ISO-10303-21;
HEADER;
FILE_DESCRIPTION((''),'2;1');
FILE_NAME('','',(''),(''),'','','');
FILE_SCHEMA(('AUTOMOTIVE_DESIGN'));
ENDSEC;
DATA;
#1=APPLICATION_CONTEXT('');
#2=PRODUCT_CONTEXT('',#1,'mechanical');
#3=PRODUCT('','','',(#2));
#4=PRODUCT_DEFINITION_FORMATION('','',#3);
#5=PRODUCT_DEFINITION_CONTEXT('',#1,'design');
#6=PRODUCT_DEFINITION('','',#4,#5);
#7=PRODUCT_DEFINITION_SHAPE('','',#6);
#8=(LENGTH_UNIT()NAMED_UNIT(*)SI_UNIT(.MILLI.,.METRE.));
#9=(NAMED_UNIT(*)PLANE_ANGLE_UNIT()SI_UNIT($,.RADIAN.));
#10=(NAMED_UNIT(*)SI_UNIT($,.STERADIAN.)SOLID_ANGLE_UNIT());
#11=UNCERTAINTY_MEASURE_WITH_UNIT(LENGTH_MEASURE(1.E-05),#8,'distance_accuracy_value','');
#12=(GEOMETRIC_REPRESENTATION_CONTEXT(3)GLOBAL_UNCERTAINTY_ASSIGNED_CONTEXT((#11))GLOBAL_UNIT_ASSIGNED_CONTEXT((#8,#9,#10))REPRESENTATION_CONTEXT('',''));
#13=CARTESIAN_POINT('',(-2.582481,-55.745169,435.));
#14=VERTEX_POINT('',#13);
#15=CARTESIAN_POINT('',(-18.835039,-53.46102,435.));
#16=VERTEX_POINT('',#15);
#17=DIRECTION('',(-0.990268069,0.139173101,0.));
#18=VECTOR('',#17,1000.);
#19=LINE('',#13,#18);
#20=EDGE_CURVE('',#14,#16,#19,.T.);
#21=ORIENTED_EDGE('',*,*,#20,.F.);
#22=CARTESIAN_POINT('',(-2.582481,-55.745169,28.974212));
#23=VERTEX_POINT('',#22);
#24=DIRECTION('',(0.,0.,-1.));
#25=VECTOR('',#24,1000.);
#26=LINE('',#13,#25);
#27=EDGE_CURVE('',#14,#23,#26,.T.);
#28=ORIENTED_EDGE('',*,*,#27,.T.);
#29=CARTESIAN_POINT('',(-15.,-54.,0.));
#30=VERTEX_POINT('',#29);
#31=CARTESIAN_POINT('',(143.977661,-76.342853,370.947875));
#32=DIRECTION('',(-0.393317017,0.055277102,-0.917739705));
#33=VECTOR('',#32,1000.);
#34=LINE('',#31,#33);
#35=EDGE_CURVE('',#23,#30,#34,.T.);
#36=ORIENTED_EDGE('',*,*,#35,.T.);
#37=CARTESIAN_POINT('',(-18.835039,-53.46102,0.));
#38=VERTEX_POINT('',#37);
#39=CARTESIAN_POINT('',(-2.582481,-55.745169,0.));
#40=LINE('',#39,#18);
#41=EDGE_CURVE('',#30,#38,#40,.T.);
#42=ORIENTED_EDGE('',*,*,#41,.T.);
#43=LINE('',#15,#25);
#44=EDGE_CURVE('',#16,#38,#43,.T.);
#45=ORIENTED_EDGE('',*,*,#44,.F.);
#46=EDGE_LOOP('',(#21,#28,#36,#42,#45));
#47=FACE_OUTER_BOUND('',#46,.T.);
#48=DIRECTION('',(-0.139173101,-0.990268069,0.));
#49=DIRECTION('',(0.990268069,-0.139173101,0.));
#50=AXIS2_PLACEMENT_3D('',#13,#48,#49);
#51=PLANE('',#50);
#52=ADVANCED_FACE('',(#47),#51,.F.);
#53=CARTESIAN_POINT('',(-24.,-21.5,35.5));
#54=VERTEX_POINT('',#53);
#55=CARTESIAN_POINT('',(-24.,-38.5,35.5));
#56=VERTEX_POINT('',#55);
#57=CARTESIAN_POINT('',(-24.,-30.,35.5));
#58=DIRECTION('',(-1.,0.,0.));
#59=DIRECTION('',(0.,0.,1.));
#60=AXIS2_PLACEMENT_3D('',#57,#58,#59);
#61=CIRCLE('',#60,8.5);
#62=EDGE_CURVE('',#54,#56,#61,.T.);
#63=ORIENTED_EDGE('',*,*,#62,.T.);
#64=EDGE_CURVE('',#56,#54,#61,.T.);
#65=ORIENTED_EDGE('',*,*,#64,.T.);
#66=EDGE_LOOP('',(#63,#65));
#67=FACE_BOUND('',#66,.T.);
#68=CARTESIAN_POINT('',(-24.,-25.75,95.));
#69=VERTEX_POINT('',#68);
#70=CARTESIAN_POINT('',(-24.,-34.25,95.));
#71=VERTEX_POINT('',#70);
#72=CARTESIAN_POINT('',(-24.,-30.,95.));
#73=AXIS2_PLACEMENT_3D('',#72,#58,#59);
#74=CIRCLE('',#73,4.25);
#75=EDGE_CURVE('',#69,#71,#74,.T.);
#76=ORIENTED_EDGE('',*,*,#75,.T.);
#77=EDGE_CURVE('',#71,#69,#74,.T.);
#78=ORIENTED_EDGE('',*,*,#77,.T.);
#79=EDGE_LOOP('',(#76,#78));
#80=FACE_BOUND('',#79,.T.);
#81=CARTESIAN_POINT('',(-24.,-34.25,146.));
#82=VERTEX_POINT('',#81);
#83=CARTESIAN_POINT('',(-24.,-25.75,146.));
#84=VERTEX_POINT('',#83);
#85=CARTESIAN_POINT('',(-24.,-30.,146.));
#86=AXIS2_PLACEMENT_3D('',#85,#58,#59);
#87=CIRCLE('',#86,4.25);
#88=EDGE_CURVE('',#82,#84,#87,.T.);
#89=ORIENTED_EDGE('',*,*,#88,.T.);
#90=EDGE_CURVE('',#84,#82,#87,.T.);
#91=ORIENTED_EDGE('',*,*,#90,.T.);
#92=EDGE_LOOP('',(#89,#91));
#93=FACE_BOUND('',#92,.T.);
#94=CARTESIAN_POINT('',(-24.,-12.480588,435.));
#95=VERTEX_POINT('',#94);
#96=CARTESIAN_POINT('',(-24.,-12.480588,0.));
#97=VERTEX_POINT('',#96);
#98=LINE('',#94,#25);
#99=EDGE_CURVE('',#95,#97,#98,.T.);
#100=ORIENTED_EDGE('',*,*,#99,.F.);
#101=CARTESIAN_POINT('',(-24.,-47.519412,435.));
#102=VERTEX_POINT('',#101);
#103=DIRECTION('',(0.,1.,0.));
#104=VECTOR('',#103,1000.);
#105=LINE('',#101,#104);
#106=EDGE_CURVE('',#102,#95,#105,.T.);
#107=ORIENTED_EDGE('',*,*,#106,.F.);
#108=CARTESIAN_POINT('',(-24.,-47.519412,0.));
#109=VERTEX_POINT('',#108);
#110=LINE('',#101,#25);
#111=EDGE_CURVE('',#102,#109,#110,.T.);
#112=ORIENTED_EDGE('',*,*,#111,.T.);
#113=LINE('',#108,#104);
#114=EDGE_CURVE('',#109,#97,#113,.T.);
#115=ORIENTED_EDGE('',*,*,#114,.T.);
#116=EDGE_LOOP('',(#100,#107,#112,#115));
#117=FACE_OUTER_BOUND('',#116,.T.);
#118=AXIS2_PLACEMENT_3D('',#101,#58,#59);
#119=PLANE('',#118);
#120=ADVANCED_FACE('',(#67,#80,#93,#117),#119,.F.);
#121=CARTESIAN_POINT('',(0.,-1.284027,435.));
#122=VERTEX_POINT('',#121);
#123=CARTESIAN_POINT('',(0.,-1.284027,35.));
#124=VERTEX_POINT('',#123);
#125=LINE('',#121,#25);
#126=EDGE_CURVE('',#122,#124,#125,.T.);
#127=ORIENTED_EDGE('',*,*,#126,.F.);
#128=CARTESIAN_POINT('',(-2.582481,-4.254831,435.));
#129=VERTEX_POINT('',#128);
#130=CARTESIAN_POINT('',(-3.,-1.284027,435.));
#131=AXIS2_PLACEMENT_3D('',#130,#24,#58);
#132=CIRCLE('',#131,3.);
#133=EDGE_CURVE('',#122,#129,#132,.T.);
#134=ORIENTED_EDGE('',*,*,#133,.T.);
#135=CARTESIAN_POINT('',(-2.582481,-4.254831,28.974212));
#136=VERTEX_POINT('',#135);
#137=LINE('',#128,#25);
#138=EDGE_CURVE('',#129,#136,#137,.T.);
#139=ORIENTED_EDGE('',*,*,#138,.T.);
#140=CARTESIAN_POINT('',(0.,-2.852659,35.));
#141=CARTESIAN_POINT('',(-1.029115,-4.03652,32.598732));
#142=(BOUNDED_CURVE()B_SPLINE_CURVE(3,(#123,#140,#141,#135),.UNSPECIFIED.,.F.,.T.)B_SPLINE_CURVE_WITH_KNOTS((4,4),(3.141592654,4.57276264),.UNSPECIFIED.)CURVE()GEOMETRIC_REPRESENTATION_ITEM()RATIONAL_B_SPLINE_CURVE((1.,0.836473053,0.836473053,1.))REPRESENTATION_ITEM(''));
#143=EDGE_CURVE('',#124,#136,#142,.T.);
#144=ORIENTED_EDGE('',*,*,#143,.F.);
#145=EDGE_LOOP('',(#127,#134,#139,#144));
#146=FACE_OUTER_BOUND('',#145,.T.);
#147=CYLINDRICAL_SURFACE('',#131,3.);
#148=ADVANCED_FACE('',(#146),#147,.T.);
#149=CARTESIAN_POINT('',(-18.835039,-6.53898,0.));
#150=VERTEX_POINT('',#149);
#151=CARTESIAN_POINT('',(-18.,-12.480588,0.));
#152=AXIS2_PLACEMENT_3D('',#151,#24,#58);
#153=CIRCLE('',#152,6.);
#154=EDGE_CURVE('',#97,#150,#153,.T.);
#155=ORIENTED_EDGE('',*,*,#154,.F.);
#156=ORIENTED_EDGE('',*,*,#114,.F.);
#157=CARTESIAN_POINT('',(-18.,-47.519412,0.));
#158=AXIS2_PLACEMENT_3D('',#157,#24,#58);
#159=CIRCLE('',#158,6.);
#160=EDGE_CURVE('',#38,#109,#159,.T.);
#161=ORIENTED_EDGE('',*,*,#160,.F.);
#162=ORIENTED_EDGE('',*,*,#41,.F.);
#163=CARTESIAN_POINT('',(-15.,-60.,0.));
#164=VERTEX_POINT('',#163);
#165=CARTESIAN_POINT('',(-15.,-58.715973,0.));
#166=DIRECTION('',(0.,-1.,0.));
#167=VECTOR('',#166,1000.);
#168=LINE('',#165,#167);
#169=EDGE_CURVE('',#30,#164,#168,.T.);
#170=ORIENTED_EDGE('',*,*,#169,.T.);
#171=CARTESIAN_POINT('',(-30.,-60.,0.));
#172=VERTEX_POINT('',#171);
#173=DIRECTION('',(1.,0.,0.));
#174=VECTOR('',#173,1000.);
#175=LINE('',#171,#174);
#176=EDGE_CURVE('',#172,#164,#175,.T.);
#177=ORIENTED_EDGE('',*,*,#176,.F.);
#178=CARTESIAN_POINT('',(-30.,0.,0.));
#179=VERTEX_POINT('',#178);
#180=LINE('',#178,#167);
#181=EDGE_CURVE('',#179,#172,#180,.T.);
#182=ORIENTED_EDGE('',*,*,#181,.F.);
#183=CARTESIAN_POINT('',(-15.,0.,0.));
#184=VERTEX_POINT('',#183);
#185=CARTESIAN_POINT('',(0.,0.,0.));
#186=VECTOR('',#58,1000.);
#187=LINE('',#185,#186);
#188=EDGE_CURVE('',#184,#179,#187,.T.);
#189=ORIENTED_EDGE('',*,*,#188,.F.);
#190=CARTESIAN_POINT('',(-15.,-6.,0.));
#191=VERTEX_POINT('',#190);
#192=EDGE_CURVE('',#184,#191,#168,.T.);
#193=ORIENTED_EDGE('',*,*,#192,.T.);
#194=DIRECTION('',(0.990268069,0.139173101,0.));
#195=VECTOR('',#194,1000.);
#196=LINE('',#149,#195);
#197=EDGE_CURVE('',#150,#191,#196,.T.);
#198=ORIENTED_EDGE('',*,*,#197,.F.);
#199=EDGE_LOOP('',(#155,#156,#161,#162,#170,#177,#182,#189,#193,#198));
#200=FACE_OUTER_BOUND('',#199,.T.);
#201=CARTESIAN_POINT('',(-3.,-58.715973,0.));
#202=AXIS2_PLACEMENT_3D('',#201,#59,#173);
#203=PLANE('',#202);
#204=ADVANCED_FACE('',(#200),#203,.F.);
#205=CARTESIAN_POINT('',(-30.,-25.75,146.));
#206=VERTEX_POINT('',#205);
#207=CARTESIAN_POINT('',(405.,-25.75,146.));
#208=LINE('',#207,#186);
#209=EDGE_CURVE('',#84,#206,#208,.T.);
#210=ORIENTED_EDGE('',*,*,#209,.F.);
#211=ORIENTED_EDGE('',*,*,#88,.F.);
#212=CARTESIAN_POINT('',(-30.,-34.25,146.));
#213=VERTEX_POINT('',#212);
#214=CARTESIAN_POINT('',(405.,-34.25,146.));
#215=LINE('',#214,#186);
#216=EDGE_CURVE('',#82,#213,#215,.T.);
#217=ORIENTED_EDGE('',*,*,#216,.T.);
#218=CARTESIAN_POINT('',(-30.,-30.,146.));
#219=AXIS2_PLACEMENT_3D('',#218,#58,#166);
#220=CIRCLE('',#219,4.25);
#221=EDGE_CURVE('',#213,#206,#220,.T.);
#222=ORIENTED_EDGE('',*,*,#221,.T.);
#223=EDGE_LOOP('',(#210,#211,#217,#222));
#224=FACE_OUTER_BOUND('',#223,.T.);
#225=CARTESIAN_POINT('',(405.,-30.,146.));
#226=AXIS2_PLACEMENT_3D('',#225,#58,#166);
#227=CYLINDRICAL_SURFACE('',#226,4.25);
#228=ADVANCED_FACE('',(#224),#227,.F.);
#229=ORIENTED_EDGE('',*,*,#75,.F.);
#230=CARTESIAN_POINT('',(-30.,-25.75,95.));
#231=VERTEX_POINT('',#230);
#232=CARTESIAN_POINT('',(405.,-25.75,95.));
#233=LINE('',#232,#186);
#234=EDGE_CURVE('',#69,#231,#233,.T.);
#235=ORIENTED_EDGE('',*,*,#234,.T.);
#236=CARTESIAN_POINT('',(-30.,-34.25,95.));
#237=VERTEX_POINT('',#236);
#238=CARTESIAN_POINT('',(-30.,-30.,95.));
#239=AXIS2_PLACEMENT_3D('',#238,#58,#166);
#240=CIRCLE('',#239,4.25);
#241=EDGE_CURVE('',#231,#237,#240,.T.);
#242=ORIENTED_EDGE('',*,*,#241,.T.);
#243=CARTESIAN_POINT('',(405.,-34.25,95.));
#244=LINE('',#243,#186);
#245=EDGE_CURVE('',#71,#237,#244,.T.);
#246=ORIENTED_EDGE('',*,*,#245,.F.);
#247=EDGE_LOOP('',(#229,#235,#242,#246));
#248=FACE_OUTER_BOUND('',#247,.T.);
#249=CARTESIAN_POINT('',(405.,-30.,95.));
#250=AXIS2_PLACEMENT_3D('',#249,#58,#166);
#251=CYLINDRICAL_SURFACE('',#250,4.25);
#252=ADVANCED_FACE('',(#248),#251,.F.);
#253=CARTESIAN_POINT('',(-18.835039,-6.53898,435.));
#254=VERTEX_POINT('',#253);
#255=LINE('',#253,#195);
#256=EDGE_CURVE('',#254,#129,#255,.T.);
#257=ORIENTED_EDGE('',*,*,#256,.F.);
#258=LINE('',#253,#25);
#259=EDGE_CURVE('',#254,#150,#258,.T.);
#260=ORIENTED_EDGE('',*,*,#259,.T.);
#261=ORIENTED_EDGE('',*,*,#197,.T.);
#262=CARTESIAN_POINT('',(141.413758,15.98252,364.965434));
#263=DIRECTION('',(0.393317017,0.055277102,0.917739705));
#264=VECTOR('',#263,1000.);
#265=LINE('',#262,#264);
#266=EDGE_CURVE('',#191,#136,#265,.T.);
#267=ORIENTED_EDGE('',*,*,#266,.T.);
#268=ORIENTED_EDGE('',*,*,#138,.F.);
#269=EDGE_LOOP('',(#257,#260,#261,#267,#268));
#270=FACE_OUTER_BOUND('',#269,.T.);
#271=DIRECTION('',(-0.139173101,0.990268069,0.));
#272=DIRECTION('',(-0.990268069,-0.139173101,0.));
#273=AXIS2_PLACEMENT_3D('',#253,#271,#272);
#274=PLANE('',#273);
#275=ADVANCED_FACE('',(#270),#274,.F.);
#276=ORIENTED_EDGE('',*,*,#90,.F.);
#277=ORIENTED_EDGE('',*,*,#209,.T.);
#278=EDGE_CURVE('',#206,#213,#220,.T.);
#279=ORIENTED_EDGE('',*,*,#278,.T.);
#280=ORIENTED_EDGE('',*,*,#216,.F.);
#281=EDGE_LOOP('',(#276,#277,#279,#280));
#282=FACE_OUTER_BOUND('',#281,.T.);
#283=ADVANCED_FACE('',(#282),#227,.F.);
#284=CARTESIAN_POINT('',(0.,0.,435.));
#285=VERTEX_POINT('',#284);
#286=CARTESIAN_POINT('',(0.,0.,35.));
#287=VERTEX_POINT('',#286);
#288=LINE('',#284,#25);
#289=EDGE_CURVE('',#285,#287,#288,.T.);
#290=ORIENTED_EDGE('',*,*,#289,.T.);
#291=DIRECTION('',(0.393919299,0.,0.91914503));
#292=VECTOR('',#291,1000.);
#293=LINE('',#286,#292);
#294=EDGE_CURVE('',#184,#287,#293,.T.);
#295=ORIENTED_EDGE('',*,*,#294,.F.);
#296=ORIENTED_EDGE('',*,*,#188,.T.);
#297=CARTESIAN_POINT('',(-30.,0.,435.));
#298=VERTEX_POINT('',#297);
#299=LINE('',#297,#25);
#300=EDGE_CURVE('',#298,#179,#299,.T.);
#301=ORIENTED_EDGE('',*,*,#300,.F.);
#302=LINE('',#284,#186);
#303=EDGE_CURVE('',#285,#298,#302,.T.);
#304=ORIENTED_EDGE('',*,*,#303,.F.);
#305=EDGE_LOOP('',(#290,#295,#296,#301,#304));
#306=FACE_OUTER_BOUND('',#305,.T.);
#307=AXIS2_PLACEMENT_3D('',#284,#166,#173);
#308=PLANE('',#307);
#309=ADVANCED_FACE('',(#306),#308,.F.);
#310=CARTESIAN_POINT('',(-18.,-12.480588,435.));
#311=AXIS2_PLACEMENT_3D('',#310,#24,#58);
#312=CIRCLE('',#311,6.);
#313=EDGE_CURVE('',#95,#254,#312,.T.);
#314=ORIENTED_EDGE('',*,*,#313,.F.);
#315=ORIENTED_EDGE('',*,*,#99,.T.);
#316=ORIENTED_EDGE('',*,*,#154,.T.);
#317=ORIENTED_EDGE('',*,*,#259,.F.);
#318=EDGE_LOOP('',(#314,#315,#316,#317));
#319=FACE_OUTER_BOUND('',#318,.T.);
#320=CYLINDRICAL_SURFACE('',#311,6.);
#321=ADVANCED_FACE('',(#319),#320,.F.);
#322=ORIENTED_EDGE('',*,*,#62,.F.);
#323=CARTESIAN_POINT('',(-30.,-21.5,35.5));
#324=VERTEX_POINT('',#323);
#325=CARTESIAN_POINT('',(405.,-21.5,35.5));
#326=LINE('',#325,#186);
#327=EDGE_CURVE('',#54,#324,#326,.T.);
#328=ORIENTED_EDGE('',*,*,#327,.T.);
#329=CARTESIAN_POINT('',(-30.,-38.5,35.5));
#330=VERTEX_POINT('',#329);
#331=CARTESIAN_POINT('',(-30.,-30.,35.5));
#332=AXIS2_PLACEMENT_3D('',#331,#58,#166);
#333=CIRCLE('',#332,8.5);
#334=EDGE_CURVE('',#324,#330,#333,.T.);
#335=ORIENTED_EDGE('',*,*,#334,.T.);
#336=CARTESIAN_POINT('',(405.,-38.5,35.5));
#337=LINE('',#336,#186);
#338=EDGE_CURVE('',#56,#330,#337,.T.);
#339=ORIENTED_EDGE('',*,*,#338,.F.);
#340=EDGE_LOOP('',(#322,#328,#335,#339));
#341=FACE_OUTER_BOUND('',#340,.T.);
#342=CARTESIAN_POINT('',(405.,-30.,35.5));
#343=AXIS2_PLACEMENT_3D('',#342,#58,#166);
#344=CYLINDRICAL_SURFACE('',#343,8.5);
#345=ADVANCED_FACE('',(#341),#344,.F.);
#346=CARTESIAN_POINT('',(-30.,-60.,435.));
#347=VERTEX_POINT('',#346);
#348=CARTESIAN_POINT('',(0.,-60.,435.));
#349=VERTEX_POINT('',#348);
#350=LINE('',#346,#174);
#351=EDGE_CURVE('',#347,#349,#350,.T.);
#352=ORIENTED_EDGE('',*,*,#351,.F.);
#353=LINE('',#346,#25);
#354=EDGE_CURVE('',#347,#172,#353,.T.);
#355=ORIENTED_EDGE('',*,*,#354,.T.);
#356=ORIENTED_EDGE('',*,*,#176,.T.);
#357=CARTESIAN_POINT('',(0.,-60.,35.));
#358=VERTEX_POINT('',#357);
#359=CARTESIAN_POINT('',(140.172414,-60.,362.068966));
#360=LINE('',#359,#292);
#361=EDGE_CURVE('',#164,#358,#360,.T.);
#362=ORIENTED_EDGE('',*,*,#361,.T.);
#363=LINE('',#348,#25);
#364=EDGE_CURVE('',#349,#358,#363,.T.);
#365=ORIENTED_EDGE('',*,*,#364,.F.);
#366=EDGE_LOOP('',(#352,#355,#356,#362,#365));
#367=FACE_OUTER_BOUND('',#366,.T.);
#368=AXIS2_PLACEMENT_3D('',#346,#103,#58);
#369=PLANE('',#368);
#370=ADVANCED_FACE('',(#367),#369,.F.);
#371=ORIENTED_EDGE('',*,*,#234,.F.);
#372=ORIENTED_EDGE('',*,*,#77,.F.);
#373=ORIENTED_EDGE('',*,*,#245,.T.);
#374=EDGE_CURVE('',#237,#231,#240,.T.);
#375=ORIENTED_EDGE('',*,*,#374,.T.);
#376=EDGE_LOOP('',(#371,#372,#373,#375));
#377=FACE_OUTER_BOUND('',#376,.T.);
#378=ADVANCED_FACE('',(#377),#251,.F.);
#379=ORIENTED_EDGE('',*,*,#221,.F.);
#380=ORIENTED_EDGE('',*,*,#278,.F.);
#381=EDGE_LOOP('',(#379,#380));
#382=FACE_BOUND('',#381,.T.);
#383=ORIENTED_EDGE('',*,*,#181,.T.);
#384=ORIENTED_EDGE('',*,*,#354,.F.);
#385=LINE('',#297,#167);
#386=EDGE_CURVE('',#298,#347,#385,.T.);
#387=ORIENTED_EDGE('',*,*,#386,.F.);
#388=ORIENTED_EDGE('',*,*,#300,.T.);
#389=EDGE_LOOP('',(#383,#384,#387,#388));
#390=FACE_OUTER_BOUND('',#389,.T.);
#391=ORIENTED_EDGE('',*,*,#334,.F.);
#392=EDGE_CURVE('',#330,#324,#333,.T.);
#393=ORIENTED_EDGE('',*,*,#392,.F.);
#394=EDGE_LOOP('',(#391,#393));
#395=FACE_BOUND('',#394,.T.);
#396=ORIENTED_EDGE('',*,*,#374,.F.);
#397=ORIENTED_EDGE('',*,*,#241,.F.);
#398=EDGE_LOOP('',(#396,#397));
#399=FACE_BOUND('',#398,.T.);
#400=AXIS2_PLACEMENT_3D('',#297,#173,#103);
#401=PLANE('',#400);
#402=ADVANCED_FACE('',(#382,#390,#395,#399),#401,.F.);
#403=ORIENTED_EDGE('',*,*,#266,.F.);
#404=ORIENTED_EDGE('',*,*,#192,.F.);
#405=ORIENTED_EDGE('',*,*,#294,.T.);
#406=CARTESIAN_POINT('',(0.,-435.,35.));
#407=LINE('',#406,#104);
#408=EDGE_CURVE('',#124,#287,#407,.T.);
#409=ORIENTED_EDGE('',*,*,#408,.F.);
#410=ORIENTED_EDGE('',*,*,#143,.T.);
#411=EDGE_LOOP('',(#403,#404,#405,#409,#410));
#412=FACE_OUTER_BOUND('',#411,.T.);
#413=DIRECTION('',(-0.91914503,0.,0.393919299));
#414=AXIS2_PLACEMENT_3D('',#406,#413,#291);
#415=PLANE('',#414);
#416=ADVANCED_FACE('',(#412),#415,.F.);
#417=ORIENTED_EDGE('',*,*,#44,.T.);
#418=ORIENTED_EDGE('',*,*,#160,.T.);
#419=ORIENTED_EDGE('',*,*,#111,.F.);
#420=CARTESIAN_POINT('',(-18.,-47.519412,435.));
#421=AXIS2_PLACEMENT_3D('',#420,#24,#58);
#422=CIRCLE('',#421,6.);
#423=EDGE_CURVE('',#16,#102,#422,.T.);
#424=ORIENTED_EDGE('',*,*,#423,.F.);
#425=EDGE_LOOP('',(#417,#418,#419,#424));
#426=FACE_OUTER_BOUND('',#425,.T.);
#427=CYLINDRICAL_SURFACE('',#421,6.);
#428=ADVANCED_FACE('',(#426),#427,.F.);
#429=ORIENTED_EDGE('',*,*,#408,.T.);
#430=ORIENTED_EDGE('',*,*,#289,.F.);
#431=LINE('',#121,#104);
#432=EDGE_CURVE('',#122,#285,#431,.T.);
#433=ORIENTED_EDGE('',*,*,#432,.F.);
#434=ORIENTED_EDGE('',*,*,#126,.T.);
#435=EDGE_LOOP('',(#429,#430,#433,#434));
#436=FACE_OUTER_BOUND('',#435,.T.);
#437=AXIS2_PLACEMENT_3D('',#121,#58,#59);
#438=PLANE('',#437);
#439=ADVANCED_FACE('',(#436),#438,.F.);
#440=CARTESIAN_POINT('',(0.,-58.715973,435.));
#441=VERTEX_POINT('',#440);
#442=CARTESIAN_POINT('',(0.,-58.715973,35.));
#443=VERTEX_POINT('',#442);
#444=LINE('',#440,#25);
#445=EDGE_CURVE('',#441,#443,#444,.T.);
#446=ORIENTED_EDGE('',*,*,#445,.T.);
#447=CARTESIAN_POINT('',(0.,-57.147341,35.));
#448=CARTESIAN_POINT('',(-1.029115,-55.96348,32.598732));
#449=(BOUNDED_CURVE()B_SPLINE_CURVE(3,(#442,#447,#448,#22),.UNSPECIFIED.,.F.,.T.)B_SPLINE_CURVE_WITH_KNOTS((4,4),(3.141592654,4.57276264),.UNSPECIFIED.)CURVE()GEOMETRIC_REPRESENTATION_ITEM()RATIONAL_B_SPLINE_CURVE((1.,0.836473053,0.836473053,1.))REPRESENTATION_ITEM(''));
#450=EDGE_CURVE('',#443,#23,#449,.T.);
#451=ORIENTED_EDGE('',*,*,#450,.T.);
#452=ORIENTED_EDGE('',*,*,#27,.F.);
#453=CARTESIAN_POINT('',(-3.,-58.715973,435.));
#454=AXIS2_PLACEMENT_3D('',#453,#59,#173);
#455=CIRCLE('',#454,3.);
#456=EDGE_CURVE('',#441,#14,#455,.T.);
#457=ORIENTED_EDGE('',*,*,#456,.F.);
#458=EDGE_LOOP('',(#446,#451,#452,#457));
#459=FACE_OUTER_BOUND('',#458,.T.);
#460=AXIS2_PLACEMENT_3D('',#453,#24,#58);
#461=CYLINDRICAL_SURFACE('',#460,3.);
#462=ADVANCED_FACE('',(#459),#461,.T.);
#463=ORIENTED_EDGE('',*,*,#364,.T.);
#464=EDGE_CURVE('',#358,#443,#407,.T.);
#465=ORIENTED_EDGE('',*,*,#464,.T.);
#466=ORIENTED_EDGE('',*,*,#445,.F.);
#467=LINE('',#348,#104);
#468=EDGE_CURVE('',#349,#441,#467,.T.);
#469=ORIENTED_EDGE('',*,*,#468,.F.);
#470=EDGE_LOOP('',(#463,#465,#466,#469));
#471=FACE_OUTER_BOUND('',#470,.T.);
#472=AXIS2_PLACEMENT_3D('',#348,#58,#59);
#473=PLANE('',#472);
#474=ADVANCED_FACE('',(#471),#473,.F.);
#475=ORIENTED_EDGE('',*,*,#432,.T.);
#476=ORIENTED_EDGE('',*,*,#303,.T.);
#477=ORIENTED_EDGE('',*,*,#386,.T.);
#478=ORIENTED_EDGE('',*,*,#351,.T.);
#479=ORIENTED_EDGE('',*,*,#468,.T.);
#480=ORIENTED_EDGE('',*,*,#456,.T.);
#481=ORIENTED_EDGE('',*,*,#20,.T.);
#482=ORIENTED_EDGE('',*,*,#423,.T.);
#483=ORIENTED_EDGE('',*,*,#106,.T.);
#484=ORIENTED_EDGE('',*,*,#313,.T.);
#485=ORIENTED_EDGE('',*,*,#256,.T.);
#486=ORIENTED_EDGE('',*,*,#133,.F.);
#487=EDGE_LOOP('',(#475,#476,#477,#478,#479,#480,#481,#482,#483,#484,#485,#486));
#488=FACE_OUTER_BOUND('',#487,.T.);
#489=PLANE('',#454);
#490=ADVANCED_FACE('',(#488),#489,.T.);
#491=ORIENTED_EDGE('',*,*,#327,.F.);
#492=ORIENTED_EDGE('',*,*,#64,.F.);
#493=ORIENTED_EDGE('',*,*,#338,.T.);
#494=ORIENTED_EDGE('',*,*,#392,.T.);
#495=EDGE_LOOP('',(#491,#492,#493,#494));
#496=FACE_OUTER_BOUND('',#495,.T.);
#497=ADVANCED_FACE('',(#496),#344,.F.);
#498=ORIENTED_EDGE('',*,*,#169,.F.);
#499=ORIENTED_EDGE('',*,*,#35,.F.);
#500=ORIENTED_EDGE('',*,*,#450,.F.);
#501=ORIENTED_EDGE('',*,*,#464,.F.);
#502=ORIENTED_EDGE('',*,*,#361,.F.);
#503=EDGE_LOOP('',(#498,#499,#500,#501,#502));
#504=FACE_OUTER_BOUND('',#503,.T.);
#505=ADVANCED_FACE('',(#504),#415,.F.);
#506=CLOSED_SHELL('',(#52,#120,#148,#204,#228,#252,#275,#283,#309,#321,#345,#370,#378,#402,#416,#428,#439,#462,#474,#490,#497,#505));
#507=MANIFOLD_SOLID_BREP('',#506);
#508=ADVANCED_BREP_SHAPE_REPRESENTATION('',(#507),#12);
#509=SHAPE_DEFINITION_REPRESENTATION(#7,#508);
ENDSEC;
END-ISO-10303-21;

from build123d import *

# Parameters (mm, degrees)
BOSS_EXTRUDE1_DEPTH = 435
SKETCH2_R           = 8.5
CUT_EXTRUDE1_DEPTH  = 435
CUT_EXTRUDE2_DEPTH  = 435
SKETCH4_R           = 4.25
CUT_EXTRUDE3_DEPTH  = 435


with BuildPart() as part:
    # Sketch1 → Boss-Extrude1 (new body)
    with BuildSketch(Plane.XY):
        with BuildLine():
            Line((0, 0), (-30, 0))
            Line((-30, 0), (-30, -60))
            Line((-30, -60), (0, -60))
            Line((0, -60), (0, -58.715972734))
            ThreePointArc((0, -58.715972734), (-0.735871259, -56.747795647), (-2.582480697, -55.745168528))
            Line((-2.582480697, -55.745168528), (-18.835038606, -53.461020473))
            ThreePointArc((-18.835038606, -53.461020473), (-22.528257481, -51.455766235), (-24, -47.519412061))
            Line((-24, -47.519412061), (-24, -12.480587939))
            ThreePointArc((-24, -12.480587939), (-22.528257481, -8.544233765), (-18.835038606, -6.538979527))
            Line((-18.835038606, -6.538979527), (-2.582480697, -4.254831472))
            ThreePointArc((-2.582480697, -4.254831472), (-0.735871259, -3.252204353), (0, -1.284027266))
            Line((0, -1.284027266), (0, 0))
        make_face()
    extrude(amount=BOSS_EXTRUDE1_DEPTH)

    # Sketch2 → Cut-Extrude1 (cut)
    with BuildSketch(Plane.ZY.offset(30)):
        with Locations(Location((35.5, -30, 0), (0, 0, 270))):
            Circle(SKETCH2_R)
    extrude(amount=-CUT_EXTRUDE1_DEPTH, mode=Mode.SUBTRACT)

    # Sketch3 → Cut-Extrude2 (cut)
    with BuildSketch(Plane(origin=(0, 0, 0), x_dir=(1, 0, 0), z_dir=(0, 1, 0))):
        Polygon((-15, 0), (0, 0), (0, -35), align=None)
    extrude(amount=-CUT_EXTRUDE2_DEPTH, mode=Mode.SUBTRACT)

    # Sketch4 → Cut-Extrude3 (cut)
    with BuildSketch(Plane.ZY.offset(30)):
        with Locations(Location((95, -30, 0), (0, 0, 270))):
            Circle(SKETCH4_R)
        with Locations(Location((146, -30, 0), (0, 0, 270))):
            Circle(SKETCH4_R)
    extrude(amount=-CUT_EXTRUDE3_DEPTH, mode=Mode.SUBTRACT)


solid = part.part
